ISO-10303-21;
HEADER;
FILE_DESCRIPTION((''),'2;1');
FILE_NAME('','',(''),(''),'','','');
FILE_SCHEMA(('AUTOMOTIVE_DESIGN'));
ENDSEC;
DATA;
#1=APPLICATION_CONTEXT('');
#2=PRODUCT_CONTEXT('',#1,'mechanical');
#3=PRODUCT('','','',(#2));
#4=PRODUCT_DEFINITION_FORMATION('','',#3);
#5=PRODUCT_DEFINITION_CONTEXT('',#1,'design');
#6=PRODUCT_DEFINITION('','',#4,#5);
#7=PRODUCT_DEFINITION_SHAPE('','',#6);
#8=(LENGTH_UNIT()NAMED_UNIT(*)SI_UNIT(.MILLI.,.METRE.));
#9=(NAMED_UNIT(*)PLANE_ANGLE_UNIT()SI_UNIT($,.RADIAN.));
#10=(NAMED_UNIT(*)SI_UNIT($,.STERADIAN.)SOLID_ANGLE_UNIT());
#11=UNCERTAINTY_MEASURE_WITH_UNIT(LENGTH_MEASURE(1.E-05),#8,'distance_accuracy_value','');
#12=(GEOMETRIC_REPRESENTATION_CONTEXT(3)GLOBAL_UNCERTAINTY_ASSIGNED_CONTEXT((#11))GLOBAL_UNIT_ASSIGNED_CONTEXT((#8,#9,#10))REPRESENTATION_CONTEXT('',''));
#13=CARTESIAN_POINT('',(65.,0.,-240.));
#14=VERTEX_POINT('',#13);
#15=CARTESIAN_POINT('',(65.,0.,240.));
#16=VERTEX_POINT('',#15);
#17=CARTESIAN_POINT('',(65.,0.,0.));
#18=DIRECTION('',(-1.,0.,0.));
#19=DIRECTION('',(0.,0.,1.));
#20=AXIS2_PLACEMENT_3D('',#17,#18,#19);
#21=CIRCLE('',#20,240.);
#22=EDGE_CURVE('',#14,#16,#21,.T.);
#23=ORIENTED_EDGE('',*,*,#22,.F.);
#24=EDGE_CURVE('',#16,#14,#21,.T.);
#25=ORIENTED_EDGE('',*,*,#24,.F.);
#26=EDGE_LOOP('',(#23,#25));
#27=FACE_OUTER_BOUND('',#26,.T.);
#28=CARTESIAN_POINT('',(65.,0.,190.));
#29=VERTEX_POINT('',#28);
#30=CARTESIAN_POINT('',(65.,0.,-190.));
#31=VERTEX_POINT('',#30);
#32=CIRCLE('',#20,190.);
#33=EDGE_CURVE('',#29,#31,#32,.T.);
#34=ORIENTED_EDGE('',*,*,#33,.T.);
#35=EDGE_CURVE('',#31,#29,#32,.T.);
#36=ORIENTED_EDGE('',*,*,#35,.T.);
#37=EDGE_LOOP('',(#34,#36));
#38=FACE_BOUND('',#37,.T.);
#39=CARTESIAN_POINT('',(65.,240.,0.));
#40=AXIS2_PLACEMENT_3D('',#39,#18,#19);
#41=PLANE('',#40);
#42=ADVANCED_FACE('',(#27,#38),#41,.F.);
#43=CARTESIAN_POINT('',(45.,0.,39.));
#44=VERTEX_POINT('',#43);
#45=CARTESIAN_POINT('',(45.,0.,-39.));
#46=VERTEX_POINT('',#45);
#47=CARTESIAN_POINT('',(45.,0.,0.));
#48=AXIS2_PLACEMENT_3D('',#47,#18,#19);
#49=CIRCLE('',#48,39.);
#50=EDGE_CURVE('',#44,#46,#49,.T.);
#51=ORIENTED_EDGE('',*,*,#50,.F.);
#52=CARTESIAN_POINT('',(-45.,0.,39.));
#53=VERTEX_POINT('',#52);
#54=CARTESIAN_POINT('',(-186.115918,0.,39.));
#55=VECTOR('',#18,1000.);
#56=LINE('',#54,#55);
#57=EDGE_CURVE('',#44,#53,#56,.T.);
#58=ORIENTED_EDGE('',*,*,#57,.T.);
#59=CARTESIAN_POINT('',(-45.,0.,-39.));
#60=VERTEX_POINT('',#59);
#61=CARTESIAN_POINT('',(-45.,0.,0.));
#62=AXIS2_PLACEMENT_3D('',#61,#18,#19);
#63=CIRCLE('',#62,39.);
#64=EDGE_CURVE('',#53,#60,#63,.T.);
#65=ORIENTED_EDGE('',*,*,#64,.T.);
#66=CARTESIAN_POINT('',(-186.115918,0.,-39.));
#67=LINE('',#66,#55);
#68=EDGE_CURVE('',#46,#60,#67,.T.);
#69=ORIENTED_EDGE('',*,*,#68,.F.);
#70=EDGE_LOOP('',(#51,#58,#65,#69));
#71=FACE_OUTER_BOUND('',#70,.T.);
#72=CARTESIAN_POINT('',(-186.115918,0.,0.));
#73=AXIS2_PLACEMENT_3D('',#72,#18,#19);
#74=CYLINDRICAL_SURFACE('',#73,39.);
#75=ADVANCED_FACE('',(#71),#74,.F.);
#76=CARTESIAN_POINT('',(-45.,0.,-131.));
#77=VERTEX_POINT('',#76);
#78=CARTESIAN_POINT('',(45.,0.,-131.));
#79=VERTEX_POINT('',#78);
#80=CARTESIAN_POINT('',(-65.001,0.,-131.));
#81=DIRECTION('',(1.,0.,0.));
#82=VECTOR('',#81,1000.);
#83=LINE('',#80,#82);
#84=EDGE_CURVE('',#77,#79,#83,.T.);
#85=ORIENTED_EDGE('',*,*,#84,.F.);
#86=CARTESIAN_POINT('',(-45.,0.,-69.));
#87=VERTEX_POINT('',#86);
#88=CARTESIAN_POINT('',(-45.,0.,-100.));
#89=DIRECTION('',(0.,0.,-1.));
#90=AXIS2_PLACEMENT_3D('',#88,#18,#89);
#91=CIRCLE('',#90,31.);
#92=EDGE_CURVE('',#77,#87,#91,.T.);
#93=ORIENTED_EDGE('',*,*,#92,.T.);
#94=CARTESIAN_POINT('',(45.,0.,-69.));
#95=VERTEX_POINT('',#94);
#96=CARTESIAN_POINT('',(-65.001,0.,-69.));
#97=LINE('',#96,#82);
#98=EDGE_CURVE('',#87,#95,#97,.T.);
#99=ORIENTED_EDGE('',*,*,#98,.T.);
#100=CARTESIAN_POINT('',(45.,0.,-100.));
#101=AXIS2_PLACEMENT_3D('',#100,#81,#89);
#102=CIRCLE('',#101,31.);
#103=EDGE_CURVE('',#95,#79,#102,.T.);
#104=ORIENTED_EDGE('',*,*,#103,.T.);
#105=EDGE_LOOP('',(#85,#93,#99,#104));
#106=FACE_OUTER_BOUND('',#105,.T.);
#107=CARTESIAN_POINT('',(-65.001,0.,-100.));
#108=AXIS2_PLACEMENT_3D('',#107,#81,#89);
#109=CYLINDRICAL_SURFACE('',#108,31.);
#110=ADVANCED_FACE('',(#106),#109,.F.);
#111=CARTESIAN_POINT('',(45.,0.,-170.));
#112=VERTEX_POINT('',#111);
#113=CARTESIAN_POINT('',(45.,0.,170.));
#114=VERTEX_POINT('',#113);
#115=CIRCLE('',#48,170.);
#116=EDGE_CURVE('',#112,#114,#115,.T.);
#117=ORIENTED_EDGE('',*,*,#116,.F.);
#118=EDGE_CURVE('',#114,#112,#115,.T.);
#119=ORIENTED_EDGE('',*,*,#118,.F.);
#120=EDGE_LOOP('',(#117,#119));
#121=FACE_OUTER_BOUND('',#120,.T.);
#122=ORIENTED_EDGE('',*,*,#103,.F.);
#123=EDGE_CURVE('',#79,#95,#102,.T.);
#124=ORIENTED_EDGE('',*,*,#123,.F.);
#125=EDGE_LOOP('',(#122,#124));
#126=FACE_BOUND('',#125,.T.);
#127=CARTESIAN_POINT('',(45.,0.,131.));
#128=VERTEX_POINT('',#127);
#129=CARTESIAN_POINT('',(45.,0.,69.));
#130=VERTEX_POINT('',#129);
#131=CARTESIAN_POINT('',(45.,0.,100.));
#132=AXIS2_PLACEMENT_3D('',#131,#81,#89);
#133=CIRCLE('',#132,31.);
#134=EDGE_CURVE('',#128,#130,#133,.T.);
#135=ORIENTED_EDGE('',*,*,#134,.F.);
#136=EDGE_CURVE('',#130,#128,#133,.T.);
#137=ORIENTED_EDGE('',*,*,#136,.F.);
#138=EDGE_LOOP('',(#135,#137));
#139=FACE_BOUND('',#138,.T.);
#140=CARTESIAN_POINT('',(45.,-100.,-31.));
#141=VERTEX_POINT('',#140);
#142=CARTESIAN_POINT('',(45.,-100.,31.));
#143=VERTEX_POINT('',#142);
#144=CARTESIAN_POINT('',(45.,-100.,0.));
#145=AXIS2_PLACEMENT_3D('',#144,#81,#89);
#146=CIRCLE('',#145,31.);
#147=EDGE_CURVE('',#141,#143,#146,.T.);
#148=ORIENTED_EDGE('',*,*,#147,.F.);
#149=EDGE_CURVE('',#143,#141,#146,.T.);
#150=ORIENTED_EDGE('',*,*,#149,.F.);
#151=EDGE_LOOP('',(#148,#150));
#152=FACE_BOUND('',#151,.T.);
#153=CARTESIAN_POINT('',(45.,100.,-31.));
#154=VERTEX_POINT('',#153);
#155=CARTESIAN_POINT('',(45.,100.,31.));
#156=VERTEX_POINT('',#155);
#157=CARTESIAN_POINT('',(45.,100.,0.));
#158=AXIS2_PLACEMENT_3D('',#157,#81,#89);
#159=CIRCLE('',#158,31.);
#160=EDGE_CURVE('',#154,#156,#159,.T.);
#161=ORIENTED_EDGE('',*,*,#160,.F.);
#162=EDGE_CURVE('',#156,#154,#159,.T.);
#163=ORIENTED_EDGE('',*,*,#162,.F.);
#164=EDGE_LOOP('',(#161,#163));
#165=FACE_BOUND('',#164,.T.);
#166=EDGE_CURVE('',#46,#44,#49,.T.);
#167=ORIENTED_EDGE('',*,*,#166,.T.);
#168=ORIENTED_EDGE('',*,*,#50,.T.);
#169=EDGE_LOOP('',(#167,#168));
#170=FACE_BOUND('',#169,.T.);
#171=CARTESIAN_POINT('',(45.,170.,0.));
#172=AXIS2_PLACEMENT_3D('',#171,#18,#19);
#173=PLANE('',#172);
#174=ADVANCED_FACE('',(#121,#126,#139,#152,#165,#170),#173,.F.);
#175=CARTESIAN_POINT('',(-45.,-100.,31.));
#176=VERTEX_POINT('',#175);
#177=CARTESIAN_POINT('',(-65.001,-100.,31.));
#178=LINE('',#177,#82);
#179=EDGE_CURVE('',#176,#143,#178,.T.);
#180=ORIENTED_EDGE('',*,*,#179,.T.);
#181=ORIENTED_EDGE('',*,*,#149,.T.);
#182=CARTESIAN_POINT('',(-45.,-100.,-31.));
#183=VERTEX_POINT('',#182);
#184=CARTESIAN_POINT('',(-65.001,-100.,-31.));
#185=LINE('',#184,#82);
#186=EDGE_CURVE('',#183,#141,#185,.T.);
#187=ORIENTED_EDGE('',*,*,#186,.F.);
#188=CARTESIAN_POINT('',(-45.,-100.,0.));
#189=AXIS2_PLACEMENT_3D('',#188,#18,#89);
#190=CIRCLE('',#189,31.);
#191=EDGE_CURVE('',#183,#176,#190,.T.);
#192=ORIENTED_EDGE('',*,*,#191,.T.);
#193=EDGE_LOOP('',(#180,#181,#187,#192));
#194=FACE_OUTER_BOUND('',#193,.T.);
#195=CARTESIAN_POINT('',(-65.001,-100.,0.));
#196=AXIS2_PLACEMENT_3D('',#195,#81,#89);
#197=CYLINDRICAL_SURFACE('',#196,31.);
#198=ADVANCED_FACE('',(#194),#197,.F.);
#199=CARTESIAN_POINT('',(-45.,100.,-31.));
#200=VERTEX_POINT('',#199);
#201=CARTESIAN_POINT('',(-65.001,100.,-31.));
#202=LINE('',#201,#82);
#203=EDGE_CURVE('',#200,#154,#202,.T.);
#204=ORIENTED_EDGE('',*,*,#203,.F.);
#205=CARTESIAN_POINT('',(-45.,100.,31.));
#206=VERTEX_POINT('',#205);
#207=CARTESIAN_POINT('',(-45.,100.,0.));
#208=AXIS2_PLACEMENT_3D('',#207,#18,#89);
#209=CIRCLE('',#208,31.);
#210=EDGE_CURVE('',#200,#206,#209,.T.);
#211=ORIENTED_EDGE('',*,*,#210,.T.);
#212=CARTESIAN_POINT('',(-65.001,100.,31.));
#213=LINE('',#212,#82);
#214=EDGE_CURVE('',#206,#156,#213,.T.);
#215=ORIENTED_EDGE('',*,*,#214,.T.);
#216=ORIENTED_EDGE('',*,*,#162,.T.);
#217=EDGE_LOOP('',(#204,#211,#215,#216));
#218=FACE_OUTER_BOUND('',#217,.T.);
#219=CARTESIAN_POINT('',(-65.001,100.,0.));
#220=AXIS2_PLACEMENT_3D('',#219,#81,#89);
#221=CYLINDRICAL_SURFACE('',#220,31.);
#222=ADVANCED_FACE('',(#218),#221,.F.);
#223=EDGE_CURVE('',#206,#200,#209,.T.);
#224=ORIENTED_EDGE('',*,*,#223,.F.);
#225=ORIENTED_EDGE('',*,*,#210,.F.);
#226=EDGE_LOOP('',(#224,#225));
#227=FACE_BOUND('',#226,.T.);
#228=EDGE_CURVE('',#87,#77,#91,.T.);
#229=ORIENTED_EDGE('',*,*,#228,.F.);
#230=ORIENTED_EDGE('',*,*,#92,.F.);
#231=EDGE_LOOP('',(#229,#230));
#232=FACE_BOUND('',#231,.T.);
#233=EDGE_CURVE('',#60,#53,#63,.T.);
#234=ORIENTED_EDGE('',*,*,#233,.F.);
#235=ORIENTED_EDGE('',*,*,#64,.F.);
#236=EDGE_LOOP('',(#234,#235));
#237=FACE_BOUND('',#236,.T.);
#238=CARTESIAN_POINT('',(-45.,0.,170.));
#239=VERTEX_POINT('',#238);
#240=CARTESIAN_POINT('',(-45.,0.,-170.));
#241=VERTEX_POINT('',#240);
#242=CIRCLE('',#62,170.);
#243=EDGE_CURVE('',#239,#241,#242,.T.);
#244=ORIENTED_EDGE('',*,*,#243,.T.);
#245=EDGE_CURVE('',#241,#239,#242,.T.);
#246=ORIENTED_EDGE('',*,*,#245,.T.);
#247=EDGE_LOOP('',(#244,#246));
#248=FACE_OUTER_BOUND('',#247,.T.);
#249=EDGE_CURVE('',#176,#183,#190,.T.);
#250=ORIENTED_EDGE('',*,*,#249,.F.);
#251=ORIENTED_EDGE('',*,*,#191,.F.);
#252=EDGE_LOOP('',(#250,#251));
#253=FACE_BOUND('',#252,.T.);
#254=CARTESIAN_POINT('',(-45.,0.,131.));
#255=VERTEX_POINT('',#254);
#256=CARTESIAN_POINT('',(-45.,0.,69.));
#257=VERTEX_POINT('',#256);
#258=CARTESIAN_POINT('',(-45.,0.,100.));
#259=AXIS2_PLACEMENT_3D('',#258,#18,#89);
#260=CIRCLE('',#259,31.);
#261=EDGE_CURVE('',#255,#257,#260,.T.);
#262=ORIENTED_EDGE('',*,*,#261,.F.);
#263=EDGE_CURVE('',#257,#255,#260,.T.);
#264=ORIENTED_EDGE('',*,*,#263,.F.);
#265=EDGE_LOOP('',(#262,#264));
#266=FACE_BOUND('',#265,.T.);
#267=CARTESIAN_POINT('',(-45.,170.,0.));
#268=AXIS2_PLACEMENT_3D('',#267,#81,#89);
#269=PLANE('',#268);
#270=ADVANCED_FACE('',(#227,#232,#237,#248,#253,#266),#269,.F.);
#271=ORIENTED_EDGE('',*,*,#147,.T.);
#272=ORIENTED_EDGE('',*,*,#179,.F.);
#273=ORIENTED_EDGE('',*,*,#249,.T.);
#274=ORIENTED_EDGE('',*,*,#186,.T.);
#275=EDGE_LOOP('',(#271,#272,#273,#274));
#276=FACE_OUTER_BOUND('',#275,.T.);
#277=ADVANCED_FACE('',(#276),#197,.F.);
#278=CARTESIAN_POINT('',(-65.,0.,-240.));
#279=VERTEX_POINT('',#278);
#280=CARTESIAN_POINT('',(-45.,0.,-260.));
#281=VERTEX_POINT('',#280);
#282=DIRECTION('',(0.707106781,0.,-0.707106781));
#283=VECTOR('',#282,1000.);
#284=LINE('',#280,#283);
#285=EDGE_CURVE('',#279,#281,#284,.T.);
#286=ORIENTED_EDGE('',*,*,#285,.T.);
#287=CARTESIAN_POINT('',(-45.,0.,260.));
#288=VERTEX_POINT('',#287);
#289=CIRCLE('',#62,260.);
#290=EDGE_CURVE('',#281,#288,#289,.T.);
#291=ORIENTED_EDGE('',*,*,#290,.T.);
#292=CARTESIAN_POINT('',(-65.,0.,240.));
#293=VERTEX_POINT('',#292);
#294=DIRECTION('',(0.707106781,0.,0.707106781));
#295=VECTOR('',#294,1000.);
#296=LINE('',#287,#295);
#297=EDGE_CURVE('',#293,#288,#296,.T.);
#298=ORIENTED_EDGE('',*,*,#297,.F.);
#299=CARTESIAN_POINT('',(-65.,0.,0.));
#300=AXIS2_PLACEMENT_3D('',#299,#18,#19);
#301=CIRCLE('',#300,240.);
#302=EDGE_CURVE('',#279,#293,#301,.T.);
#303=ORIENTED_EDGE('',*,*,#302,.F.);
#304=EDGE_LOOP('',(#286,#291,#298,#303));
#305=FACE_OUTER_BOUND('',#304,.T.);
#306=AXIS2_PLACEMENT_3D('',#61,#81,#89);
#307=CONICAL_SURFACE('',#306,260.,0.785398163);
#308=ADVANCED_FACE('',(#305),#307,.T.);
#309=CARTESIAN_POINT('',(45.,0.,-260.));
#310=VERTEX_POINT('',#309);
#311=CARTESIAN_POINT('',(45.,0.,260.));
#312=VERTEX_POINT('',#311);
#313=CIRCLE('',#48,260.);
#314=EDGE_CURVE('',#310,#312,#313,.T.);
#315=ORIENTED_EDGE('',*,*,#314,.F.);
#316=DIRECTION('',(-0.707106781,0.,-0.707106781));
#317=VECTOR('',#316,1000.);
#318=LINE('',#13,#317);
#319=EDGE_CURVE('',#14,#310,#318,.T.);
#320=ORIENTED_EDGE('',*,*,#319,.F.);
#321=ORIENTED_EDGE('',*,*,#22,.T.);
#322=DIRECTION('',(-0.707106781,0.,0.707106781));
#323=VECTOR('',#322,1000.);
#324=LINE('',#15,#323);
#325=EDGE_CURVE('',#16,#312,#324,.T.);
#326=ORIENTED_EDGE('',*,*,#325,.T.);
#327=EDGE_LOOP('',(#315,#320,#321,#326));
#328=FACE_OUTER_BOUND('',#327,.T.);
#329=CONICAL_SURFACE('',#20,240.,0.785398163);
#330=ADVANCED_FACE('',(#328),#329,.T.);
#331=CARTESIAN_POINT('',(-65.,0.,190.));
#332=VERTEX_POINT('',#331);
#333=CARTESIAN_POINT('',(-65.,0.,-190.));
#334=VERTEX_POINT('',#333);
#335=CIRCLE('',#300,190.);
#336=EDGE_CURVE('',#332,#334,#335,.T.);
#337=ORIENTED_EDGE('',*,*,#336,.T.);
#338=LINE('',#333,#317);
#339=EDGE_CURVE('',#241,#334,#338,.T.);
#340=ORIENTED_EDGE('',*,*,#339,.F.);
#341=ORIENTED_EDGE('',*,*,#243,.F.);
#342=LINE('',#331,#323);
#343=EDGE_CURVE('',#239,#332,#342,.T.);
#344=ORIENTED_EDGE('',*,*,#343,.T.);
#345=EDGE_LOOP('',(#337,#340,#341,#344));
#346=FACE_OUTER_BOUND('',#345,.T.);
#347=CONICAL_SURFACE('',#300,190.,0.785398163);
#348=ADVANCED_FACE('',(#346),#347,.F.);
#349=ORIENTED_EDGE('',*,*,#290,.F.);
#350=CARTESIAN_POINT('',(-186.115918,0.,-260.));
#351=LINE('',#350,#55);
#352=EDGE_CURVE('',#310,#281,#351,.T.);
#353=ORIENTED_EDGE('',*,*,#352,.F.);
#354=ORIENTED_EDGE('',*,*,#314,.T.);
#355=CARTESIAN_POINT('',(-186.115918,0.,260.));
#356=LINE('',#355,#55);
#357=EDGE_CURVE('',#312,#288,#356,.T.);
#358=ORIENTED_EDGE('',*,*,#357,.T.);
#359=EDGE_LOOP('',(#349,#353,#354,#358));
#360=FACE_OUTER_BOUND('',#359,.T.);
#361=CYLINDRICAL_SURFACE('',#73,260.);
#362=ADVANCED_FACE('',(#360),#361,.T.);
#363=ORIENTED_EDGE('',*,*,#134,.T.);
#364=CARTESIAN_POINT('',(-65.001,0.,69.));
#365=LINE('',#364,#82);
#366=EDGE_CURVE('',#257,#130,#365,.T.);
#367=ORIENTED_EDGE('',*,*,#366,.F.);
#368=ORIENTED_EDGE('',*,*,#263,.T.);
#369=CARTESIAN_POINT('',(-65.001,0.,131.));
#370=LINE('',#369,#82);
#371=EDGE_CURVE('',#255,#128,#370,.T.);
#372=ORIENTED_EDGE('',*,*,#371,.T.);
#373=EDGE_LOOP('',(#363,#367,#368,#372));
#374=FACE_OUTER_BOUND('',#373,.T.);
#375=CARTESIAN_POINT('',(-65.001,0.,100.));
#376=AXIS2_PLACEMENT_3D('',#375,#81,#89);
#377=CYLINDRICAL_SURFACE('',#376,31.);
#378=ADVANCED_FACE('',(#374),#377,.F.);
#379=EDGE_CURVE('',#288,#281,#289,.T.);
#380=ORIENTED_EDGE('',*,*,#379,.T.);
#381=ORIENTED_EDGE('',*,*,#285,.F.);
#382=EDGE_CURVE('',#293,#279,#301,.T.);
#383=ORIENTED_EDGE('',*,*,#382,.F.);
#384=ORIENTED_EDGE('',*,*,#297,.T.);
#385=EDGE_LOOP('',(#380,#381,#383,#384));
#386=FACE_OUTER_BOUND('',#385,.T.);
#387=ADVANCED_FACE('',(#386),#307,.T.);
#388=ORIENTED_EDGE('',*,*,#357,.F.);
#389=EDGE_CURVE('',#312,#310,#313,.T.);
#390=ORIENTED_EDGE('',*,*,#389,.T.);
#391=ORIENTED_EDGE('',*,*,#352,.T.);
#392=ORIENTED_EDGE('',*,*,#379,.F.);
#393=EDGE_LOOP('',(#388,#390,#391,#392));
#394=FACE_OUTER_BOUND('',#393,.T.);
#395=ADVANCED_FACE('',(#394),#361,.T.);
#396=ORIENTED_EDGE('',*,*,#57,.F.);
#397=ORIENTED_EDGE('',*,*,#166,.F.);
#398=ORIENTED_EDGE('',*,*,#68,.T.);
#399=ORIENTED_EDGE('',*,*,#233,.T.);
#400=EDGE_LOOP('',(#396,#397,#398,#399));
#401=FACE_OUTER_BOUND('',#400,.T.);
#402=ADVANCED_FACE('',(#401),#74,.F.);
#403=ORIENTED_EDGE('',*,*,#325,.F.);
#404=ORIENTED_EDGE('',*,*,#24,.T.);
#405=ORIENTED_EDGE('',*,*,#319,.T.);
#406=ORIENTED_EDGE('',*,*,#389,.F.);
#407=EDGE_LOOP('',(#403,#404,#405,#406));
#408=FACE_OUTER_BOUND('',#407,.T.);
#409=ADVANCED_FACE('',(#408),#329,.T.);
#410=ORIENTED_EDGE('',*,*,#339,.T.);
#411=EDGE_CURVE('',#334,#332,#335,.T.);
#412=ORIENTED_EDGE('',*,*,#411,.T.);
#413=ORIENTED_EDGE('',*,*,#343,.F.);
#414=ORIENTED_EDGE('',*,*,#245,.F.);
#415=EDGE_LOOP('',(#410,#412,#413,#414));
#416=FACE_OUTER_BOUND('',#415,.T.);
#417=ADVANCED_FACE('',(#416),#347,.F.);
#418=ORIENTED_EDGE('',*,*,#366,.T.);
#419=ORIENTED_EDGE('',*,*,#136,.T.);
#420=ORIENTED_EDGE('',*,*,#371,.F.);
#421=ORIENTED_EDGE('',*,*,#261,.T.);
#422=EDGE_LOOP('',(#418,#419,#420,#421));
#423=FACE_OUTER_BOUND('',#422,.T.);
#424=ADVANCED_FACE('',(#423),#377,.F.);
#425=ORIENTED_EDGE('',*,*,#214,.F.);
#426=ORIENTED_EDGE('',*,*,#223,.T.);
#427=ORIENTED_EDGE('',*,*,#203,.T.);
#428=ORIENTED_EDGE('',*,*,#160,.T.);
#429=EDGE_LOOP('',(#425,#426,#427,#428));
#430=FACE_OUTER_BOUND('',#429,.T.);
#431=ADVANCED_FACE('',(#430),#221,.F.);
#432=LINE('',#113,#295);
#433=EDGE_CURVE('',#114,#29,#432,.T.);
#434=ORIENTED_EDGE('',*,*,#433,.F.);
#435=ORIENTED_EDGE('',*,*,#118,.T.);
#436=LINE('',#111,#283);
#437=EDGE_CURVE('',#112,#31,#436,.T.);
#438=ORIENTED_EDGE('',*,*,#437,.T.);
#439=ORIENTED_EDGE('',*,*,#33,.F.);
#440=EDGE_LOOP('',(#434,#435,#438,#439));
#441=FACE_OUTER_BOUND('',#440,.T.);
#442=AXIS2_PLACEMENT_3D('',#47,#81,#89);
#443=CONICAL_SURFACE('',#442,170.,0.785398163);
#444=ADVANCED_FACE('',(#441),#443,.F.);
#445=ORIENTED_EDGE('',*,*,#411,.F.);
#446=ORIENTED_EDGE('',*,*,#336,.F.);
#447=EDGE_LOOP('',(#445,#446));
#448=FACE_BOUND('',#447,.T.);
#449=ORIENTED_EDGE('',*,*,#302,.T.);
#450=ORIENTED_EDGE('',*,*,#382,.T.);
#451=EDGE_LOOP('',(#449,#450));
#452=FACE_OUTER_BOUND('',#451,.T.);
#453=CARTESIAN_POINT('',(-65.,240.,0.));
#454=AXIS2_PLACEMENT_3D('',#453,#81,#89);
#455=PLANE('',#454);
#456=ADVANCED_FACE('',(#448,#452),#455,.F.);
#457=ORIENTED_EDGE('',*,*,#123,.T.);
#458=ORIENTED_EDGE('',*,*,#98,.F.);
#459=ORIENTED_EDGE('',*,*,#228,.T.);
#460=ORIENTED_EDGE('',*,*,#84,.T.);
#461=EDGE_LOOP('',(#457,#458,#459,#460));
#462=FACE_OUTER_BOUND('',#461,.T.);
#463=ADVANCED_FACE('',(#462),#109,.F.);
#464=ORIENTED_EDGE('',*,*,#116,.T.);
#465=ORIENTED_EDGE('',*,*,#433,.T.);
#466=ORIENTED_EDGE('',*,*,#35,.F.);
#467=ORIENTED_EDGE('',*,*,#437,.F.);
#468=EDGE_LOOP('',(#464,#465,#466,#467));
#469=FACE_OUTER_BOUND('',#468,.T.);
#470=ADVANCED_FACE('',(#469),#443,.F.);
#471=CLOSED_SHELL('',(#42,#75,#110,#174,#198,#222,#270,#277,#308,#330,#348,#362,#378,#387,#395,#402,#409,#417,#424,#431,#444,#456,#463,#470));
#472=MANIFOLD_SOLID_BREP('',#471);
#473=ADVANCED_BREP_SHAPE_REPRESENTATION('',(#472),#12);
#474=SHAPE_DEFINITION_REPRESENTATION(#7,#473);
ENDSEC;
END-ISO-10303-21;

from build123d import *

# Parameters (mm, degrees)
THREAD_HOLES_5X_REACH = 385.797
THREAD_HOLES_SKETCH_R = 31


with BuildPart() as part:
    # Disc Profile Sketch → Button Disc Body (revolve)
    with BuildSketch(Plane.XY, mode=Mode.PRIVATE) as button_disc_body_sk:
        Polygon((-45, 260), (-65, 240), (-65, 190), (-45, 170), (-45, 39), (45, 39), (45, 170), (65, 190), (65, 240), (45, 260), align=None)
    revolve(button_disc_body_sk.sketch.rotate(Axis((-186.115918114, 0, 0), (1, 0, 0)), 90), axis=Axis((-186.115918114, 0, 0), (1, 0, 0)))

    # Thread Holes Sketch → Thread Holes 5x (cut, up to next)
    with BuildSketch(Plane(origin=(45, 0, 0), x_dir=(0, 0, -1), z_dir=(1, 0, 0)), mode=Mode.PRIVATE) as thread_holes_5x_sk1:
        with Locations((0, 100)):
            Circle(THREAD_HOLES_SKETCH_R)
    thread_holes_5x_tool1 = extrude(thread_holes_5x_sk1.sketch, amount=-THREAD_HOLES_5X_REACH, mode=Mode.PRIVATE) & part.part
    # Thread Holes Sketch → Thread Holes 5x (cut, up to next)
    with BuildSketch(Plane(origin=(45, 0, 0), x_dir=(0, 0, -1), z_dir=(1, 0, 0)), mode=Mode.PRIVATE) as thread_holes_5x_sk2:
        with Locations((100, 0)):
            Circle(THREAD_HOLES_SKETCH_R)
    thread_holes_5x_tool2 = extrude(thread_holes_5x_sk2.sketch, amount=-THREAD_HOLES_5X_REACH, mode=Mode.PRIVATE) & part.part
    # Thread Holes Sketch → Thread Holes 5x (cut, up to next)
    with BuildSketch(Plane(origin=(45, 0, 0), x_dir=(0, 0, -1), z_dir=(1, 0, 0)), mode=Mode.PRIVATE) as thread_holes_5x_sk3:
        with Locations((0, -100)):
            Circle(THREAD_HOLES_SKETCH_R)
    thread_holes_5x_tool3 = extrude(thread_holes_5x_sk3.sketch, amount=-THREAD_HOLES_5X_REACH, mode=Mode.PRIVATE) & part.part
    # Thread Holes Sketch → Thread Holes 5x (cut, up to next)
    with BuildSketch(Plane(origin=(45, 0, 0), x_dir=(0, 0, -1), z_dir=(1, 0, 0)), mode=Mode.PRIVATE) as thread_holes_5x_sk4:
        with Locations((-100, 0)):
            Circle(THREAD_HOLES_SKETCH_R)
    thread_holes_5x_tool4 = extrude(thread_holes_5x_sk4.sketch, amount=-THREAD_HOLES_5X_REACH, mode=Mode.PRIVATE) & part.part
    add(thread_holes_5x_tool1.solids().sort_by_distance((45, 100, 0))[0], mode=Mode.SUBTRACT)
    add(thread_holes_5x_tool2.solids().sort_by_distance((45, 0, -100))[0], mode=Mode.SUBTRACT)
    add(thread_holes_5x_tool3.solids().sort_by_distance((45, -100, 0))[0], mode=Mode.SUBTRACT)
    add(thread_holes_5x_tool4.solids().sort_by_distance((45, 0, 100))[0], mode=Mode.SUBTRACT)


solid = part.part
